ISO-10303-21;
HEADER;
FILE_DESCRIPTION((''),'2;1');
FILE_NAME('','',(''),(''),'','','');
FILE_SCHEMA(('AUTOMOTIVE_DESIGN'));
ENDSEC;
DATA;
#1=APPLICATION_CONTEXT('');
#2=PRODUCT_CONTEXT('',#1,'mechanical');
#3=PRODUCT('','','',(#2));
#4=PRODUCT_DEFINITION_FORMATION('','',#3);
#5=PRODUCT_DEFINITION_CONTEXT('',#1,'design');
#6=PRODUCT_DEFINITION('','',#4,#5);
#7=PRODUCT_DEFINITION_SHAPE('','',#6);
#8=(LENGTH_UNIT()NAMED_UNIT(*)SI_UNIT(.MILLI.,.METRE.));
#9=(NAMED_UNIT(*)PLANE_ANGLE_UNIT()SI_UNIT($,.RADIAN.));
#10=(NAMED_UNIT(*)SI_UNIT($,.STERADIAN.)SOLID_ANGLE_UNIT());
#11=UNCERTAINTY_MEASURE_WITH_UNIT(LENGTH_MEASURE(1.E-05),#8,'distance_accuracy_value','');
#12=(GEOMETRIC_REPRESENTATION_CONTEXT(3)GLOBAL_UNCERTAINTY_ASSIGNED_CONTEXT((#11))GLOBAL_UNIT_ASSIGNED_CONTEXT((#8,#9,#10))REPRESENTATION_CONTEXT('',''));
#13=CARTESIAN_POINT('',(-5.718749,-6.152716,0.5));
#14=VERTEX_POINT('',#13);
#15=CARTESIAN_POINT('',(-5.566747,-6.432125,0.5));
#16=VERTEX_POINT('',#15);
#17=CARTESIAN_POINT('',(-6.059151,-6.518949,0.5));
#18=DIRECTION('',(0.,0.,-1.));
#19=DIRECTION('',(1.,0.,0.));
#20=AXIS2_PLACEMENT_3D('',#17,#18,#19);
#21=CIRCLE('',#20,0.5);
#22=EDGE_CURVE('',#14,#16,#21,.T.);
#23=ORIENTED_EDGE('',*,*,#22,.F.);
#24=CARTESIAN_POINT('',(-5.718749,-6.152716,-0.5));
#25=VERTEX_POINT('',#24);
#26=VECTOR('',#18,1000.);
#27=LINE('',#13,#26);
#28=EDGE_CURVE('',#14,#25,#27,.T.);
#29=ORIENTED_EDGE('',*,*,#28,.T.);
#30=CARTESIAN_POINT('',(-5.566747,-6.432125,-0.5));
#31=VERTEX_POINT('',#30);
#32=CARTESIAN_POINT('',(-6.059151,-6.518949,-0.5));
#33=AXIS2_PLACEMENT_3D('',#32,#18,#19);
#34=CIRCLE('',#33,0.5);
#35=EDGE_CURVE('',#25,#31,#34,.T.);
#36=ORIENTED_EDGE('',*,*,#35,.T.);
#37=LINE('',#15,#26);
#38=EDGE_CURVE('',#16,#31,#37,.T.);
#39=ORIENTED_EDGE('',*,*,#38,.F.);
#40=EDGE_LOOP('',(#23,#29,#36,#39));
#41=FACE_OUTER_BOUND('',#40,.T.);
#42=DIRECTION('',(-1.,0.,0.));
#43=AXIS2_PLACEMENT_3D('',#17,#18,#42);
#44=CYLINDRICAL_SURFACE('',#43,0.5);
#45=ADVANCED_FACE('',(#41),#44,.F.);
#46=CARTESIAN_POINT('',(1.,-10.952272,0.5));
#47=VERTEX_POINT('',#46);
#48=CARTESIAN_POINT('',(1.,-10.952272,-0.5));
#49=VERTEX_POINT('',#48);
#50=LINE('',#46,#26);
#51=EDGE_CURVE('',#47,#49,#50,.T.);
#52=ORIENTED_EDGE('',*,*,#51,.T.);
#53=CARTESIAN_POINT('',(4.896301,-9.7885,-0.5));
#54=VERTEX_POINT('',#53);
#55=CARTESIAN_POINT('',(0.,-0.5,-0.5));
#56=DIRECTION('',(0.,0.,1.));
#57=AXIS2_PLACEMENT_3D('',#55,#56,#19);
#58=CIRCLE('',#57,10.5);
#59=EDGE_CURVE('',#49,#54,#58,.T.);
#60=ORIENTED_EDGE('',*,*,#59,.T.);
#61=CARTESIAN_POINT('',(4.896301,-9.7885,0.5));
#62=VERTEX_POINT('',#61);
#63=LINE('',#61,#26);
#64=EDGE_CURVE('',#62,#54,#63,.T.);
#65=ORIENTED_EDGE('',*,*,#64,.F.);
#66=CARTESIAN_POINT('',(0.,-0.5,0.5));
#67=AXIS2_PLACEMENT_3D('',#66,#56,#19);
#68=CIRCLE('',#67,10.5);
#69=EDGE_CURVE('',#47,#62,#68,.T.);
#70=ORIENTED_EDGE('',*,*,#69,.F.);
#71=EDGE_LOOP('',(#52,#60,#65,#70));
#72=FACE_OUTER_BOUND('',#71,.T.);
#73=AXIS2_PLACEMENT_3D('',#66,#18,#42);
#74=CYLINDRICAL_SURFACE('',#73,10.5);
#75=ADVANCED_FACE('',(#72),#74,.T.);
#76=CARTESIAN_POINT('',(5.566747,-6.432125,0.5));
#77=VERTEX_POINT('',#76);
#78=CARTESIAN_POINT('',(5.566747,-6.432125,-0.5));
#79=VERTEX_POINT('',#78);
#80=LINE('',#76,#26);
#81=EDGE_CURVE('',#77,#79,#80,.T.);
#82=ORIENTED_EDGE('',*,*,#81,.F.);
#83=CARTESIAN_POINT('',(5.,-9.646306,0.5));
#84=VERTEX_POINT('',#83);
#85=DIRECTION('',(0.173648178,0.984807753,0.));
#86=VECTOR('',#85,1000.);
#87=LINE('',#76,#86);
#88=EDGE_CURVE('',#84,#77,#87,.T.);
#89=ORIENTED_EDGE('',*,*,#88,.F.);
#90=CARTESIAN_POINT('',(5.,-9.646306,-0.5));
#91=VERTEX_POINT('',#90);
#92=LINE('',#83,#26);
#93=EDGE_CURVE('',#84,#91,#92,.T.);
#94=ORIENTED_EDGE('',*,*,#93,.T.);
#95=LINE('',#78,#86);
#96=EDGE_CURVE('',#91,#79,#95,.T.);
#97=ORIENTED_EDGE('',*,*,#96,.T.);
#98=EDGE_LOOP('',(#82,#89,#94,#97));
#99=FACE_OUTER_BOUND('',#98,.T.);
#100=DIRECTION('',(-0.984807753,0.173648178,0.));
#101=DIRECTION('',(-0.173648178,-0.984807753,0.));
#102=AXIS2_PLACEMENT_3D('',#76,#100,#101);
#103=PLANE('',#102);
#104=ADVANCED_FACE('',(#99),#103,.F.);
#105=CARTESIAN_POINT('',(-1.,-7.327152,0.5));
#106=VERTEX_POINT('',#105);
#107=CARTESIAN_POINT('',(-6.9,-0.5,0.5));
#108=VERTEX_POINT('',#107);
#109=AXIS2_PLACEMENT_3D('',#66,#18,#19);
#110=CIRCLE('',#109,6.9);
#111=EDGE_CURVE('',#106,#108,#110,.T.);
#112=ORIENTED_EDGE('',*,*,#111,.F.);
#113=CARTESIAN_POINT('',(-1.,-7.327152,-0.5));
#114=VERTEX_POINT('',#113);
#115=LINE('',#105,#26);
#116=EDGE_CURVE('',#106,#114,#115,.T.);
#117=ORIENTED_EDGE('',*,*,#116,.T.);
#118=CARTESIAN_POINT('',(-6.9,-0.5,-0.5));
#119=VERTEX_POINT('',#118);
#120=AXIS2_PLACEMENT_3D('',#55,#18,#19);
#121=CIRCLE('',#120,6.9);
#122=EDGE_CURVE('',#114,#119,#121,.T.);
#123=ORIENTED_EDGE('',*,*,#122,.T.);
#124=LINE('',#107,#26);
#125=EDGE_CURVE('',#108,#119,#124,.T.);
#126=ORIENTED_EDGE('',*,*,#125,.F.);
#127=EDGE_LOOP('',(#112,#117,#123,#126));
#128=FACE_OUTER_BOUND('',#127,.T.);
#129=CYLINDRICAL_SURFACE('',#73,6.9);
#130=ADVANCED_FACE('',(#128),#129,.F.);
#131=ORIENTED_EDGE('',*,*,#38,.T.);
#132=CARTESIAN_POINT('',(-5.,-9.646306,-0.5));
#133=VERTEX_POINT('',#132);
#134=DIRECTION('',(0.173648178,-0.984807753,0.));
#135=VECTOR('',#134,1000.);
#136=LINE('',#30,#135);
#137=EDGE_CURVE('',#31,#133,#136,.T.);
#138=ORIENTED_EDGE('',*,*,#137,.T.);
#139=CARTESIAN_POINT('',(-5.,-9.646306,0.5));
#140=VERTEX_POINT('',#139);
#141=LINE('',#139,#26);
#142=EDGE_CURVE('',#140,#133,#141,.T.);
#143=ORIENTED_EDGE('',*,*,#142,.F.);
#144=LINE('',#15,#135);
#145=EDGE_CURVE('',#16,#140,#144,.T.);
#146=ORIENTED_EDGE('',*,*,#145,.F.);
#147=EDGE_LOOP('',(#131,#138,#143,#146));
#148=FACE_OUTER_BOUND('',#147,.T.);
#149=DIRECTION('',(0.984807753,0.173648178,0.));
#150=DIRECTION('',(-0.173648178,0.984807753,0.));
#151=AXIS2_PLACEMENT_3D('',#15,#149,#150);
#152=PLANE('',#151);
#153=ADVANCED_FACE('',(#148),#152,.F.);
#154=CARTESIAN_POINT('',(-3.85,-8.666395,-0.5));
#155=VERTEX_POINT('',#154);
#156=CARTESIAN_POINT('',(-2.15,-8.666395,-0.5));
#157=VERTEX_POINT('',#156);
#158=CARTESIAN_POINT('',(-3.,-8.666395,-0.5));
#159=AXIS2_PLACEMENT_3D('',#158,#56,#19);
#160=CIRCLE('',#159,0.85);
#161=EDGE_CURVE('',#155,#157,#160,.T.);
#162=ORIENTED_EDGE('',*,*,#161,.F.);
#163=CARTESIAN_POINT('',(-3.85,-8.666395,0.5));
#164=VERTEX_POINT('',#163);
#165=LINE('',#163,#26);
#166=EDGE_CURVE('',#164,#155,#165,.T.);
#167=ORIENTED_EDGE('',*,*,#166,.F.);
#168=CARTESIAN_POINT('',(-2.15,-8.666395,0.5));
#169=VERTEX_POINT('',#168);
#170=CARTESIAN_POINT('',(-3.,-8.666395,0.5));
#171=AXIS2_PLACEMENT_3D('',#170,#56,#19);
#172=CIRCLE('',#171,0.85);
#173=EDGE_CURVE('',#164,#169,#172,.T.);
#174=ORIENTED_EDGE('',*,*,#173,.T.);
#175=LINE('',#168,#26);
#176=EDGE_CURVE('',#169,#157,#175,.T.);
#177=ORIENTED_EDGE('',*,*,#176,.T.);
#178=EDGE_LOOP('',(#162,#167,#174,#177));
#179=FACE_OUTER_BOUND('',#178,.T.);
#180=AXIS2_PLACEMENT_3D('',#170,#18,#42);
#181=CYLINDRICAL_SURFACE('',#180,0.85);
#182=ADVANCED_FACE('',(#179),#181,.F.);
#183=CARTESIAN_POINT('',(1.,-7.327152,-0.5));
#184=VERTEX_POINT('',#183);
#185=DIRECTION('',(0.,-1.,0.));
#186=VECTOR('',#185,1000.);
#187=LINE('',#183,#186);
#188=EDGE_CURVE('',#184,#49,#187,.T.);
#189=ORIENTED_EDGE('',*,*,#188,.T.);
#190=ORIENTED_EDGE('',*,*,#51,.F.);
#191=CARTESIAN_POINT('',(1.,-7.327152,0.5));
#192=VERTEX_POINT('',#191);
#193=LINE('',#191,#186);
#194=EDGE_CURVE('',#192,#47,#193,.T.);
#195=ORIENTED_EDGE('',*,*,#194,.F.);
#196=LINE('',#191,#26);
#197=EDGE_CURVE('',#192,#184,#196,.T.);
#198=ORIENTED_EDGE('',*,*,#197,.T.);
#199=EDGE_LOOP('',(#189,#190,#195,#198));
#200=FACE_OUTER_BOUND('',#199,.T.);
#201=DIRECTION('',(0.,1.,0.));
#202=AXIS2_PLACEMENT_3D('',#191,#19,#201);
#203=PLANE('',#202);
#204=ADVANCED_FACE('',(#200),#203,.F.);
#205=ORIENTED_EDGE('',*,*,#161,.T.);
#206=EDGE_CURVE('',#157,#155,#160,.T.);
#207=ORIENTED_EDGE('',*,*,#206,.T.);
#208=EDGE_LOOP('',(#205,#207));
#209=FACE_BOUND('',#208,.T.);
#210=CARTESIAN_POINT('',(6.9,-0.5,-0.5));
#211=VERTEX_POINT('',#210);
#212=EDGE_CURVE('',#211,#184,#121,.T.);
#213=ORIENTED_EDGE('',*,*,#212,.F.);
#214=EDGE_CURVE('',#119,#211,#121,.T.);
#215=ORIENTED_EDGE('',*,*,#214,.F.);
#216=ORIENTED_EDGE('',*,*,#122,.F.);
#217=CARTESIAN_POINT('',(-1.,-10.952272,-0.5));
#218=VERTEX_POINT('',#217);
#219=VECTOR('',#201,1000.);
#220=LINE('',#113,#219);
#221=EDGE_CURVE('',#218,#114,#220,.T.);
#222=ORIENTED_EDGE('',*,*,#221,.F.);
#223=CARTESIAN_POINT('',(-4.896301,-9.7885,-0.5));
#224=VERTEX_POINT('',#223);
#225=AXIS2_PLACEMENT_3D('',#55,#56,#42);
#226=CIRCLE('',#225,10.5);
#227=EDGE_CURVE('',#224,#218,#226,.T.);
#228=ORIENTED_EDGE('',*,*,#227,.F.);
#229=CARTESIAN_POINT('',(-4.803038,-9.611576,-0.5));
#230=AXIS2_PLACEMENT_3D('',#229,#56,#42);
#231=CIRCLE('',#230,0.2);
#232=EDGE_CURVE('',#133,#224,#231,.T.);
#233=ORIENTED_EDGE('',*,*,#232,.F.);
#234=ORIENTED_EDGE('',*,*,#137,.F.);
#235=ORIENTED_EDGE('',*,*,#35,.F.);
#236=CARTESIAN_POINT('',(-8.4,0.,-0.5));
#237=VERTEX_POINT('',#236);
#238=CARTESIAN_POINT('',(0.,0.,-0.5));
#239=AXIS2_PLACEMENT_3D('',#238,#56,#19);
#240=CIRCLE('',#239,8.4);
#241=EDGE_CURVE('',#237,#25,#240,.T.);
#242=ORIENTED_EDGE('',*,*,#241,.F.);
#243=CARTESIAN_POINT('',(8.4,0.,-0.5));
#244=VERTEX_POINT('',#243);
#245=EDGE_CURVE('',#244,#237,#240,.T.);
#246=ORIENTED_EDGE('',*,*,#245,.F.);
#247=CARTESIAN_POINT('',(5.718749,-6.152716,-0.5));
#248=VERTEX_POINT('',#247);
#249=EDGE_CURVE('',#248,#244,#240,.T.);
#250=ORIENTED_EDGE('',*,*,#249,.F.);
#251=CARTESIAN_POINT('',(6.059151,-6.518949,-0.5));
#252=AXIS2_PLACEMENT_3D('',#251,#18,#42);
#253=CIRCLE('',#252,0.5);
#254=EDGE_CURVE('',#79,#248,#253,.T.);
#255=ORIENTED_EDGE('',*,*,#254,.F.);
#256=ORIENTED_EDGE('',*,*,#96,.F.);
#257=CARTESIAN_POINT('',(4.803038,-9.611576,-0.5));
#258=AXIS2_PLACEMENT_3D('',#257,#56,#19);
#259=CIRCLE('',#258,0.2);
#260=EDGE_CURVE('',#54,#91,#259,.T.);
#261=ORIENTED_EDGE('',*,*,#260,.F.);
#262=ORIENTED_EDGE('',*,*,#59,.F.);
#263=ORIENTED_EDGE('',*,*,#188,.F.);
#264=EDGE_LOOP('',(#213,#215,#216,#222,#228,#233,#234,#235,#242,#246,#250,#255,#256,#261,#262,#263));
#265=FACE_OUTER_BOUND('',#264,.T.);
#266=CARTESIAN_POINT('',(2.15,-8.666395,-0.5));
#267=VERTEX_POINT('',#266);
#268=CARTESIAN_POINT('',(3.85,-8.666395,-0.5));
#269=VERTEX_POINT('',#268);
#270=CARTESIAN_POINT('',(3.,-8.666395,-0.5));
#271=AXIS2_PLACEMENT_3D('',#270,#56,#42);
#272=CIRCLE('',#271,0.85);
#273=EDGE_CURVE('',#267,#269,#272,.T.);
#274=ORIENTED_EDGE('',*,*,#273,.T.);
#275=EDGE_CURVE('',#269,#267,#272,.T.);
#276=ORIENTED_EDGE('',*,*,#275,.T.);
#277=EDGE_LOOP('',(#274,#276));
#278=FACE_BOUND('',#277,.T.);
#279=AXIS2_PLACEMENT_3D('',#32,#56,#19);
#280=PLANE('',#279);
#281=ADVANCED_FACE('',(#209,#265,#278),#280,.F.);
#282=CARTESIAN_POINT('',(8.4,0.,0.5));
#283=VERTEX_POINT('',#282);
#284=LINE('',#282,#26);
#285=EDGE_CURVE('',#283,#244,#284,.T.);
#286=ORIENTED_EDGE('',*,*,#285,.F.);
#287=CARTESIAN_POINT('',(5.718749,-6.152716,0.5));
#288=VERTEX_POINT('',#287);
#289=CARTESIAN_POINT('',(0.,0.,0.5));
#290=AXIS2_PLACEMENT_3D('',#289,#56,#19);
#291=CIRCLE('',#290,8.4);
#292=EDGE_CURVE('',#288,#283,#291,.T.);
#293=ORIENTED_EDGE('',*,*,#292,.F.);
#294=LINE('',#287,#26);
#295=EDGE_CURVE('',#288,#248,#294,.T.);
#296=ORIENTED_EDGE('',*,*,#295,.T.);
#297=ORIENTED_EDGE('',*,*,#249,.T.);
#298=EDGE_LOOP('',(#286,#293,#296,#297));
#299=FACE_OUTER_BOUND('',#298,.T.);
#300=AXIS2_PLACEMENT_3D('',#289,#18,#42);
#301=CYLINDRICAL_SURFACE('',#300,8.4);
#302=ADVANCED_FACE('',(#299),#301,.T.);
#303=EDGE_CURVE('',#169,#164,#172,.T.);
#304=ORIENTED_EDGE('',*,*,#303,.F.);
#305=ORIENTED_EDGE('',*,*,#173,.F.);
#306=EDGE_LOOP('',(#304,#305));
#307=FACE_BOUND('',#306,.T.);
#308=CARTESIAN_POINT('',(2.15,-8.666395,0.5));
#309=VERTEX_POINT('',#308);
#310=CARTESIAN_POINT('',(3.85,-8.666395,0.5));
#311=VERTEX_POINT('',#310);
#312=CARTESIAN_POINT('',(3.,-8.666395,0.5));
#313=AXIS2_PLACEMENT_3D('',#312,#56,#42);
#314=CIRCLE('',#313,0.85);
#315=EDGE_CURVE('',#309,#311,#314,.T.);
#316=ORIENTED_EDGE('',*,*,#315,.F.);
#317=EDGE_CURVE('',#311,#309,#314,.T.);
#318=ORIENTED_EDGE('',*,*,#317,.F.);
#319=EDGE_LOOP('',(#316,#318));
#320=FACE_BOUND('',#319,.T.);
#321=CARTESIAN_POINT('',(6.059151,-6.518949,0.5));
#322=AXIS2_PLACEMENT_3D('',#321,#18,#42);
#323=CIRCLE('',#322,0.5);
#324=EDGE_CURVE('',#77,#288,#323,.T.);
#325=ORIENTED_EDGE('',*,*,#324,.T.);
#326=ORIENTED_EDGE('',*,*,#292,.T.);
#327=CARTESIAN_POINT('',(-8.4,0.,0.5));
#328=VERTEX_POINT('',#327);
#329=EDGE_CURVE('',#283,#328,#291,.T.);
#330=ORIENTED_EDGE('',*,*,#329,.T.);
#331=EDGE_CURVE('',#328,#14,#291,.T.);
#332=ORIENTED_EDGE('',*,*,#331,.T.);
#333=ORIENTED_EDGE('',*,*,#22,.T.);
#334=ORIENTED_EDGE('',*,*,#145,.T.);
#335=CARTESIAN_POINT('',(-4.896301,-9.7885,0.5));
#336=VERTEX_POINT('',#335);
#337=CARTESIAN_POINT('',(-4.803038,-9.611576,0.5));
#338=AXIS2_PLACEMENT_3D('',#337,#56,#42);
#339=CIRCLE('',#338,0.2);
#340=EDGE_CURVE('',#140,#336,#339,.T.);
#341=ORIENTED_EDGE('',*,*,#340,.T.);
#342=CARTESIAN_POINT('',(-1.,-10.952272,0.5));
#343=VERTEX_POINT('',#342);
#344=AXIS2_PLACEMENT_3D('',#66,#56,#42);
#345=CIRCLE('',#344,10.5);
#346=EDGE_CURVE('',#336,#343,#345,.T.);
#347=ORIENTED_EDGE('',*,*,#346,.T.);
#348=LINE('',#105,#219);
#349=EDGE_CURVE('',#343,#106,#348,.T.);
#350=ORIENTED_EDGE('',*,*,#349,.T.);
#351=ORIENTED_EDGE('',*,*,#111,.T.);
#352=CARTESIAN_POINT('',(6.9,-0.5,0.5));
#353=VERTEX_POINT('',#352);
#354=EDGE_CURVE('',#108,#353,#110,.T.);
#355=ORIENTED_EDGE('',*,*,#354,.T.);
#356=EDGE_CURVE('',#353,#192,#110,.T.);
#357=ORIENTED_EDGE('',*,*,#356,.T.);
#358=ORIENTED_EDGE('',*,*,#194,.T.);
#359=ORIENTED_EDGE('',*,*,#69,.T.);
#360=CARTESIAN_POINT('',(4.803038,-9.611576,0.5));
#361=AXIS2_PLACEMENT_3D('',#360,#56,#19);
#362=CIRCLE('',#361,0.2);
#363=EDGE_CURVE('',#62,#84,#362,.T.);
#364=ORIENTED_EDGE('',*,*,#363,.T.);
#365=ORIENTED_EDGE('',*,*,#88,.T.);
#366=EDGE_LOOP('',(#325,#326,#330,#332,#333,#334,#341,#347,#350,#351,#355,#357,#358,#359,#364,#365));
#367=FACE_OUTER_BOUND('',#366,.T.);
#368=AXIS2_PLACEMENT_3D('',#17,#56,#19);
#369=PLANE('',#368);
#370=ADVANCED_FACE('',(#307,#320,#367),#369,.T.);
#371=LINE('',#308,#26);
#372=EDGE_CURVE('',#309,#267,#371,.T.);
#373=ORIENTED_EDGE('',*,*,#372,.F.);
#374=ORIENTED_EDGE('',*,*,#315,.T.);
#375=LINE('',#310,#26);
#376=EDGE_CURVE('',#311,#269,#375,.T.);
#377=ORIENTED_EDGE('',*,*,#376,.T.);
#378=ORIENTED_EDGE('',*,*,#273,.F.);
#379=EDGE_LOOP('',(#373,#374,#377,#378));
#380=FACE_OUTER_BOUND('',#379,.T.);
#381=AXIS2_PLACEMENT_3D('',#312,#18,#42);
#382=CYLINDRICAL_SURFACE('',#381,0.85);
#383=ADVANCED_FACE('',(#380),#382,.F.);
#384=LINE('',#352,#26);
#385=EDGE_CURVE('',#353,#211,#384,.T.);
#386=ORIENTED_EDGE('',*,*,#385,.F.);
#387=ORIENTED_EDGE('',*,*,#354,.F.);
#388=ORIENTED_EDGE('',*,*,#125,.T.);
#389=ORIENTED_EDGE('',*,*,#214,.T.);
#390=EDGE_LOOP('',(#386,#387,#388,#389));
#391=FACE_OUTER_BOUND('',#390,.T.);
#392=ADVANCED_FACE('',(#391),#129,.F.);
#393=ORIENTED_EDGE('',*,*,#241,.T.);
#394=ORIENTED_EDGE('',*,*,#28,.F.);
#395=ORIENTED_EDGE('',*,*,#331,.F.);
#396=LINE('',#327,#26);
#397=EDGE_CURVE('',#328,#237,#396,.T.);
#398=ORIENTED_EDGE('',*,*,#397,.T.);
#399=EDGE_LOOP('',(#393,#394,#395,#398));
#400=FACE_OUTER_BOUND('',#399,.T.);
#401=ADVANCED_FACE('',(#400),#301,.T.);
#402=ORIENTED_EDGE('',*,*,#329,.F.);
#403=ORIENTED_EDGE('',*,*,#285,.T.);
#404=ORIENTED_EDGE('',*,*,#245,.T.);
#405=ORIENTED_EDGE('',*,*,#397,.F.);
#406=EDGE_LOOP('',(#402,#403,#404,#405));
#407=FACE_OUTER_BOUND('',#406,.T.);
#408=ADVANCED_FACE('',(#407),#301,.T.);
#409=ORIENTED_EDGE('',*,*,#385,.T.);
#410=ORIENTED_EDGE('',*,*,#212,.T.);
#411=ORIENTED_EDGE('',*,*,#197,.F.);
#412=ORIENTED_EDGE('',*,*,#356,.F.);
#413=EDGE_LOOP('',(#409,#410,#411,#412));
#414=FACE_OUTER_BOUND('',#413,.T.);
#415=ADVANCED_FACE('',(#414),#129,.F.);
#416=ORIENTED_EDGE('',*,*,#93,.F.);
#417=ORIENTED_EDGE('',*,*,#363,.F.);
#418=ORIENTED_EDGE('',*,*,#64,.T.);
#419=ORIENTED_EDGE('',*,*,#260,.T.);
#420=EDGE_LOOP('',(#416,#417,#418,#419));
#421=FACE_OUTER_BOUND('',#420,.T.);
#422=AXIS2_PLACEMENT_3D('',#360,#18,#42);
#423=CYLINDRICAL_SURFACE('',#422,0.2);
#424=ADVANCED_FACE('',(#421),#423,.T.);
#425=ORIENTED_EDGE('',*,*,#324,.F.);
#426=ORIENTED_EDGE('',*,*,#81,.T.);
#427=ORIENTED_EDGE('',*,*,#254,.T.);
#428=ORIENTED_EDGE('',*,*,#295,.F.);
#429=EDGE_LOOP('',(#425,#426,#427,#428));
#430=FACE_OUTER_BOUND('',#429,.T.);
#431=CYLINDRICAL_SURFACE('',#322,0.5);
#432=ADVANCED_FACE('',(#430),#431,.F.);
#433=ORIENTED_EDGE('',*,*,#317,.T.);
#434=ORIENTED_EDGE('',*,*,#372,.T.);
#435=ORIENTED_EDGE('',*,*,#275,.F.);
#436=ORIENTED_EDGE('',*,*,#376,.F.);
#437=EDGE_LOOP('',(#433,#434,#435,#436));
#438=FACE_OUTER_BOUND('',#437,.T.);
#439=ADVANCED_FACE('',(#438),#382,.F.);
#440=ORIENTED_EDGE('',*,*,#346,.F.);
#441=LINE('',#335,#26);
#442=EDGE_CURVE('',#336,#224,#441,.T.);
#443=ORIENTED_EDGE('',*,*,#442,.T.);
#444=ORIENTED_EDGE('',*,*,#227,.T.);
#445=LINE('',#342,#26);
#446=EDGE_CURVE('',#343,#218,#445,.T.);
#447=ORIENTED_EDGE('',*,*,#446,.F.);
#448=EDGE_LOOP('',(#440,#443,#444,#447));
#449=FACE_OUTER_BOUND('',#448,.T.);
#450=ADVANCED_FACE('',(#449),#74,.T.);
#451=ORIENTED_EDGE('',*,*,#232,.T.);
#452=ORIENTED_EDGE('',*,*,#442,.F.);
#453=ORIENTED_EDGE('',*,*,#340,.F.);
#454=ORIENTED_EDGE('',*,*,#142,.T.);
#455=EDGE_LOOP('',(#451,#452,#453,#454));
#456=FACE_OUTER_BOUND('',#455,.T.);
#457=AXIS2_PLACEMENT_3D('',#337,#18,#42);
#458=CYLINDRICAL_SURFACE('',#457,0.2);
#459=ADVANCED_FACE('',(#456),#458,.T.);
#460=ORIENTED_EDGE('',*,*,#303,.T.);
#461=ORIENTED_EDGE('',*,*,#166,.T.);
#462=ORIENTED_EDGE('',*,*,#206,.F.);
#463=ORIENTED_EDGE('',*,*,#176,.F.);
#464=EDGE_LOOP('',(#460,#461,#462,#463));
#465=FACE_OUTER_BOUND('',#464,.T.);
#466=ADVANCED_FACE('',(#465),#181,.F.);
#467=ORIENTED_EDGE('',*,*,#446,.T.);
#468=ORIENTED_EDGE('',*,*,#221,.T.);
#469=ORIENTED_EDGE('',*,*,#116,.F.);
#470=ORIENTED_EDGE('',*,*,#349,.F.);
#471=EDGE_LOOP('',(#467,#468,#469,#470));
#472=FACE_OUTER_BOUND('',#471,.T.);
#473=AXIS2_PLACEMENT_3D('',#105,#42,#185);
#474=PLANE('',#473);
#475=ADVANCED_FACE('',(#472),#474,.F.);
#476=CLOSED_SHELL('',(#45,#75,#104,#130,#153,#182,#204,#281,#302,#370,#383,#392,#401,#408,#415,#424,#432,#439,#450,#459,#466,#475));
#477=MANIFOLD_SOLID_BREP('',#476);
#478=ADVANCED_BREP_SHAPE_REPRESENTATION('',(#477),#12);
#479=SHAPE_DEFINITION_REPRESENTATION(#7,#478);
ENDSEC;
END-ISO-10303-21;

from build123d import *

# Parameters (mm, degrees)
EXTRUDE_972_DEPTH      = 0.5
EXTRUDE_972_DEPTH_BACK = 0.5
SKETCH_1_R             = 0.85


with BuildPart() as part:
    # 草图1 → Extrude 972 (new, two sides: drawn at the far end of the back side and taken through both)
    with BuildSketch(Plane.XY.offset(-EXTRUDE_972_DEPTH_BACK)):
        with BuildLine():
            Line((-1, -7.327151675), (-1, -10.95227248))
            ThreePointArc((-1, -10.95227248), (-3.005026441, -10.560805936), (-4.896301332, -9.788500055))
            ThreePointArc((-4.896301332, -9.788500055), (-4.964631615, -9.729422113), (-5, -9.64630588))
            Line((-5, -9.64630588), (-5.566746879, -6.432124609))
            ThreePointArc((-5.566746879, -6.432124609), (-5.619937096, -6.280010711), (-5.718749028, -6.152715625))
            ThreePointArc((-5.718749028, -6.152715625), (0, 8.4), (5.718749028, -6.152715625))
            ThreePointArc((5.718749028, -6.152715625), (5.619937096, -6.280010711), (5.566746879, -6.432124609))
            Line((5.566746879, -6.432124609), (5, -9.64630588))
            ThreePointArc((5, -9.64630588), (4.964631615, -9.729422113), (4.896301332, -9.788500055))
            ThreePointArc((4.896301332, -9.788500055), (3.005026441, -10.560805936), (1, -10.95227248))
            Line((1, -10.95227248), (1, -7.327151675))
            ThreePointArc((1, -7.327151675), (0, 6.4), (-1, -7.327151675))
        make_face()
        with Locations((-3, -8.666394553)):
            Circle(SKETCH_1_R, mode=Mode.SUBTRACT)
        with Locations(Location((3, -8.666394553, 0), (0, 0, 180))):
            Circle(SKETCH_1_R, mode=Mode.SUBTRACT)
    extrude(amount=EXTRUDE_972_DEPTH + EXTRUDE_972_DEPTH_BACK)


solid = part.part
